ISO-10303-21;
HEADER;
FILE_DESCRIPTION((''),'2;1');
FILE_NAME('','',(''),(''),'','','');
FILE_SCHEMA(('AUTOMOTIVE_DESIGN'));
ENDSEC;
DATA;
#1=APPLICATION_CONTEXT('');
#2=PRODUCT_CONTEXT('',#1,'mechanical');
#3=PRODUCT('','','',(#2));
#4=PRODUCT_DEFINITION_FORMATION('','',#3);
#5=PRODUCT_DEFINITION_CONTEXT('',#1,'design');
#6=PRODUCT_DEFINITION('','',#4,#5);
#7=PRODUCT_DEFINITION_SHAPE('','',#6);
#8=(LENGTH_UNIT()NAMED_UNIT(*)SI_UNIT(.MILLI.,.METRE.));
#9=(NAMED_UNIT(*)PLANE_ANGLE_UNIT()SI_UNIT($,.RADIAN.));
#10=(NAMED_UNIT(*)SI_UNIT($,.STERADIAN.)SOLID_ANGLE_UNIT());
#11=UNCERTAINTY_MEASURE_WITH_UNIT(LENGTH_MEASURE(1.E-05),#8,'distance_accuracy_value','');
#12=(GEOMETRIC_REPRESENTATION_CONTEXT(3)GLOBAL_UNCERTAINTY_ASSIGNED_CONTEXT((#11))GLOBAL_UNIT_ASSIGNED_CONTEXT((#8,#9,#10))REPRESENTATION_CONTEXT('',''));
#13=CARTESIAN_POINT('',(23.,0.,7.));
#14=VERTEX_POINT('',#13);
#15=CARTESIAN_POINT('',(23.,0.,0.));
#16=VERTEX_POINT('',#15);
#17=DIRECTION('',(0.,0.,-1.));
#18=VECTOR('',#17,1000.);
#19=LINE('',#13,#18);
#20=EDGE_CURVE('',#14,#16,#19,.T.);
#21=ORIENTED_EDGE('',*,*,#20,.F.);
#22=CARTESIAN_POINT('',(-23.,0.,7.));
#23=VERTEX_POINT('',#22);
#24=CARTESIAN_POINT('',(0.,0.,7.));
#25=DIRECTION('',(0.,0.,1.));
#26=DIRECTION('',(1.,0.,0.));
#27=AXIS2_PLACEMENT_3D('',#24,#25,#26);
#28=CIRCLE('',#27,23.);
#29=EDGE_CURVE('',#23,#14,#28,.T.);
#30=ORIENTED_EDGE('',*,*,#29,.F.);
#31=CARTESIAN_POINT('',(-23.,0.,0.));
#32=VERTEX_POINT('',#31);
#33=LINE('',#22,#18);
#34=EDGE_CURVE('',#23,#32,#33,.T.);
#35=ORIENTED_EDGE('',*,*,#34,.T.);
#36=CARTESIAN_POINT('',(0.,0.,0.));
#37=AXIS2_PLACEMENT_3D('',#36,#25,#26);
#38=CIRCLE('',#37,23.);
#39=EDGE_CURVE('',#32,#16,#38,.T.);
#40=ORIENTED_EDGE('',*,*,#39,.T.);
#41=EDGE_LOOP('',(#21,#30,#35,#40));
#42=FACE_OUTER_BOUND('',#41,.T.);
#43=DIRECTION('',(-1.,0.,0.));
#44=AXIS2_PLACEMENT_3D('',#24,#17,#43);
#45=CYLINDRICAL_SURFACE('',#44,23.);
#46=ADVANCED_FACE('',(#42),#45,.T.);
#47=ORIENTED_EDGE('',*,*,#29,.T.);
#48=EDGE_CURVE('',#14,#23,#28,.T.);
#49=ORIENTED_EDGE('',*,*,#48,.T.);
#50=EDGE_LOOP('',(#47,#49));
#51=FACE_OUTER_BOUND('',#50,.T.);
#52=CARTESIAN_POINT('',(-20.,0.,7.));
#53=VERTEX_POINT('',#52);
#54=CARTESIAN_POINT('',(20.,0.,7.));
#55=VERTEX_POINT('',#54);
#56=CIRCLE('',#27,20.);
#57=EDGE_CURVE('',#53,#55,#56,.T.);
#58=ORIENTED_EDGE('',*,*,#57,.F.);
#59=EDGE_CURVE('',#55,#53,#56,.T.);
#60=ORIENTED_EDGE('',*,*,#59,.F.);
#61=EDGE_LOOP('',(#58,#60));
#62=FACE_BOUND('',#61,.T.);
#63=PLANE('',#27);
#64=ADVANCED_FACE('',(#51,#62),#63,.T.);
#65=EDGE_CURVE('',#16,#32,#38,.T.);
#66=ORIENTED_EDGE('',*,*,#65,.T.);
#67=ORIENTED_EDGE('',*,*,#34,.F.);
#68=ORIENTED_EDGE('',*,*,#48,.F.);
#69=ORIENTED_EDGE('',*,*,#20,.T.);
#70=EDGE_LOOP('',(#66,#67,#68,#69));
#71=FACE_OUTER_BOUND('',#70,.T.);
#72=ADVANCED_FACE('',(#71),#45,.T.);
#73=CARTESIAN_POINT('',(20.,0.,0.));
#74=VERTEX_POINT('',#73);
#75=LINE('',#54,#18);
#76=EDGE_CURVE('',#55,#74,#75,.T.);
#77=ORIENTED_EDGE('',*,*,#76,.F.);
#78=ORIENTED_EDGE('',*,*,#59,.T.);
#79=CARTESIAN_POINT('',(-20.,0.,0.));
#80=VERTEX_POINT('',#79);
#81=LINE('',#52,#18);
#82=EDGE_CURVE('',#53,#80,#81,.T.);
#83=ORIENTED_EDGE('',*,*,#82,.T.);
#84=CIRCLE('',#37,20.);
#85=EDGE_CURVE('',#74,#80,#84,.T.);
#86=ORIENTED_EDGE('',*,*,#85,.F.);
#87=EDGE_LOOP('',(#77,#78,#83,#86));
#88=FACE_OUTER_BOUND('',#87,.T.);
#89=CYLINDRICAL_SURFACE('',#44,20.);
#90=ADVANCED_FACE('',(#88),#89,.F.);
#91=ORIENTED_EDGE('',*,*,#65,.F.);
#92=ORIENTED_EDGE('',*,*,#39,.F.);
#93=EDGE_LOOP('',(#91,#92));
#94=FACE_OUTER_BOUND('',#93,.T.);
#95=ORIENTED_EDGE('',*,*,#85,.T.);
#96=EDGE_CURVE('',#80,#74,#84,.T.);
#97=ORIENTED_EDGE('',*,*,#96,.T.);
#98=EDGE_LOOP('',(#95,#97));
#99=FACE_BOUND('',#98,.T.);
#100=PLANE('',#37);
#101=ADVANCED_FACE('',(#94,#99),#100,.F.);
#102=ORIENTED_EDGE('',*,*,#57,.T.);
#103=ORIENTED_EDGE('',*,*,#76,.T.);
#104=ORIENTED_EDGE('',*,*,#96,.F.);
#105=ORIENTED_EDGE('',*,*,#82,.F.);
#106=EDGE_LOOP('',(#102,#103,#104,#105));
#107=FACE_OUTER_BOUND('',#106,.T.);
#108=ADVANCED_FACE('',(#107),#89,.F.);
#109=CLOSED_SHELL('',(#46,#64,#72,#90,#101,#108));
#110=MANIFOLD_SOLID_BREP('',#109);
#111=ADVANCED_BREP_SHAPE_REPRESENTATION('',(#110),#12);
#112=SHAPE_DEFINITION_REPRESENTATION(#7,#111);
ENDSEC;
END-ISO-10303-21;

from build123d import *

# Parameters (mm, degrees)
SKETCH_1_R      = 23
SKETCH_1_R_2    = 20
EXTRUDE_1_DEPTH = 7


with BuildPart() as part:
    # 草图1 → 凸台-拉伸1 (new body)
    with BuildSketch(Plane.XY):
        Circle(SKETCH_1_R)
        Circle(SKETCH_1_R_2, mode=Mode.SUBTRACT)
    extrude(amount=EXTRUDE_1_DEPTH)


solid = part.part
